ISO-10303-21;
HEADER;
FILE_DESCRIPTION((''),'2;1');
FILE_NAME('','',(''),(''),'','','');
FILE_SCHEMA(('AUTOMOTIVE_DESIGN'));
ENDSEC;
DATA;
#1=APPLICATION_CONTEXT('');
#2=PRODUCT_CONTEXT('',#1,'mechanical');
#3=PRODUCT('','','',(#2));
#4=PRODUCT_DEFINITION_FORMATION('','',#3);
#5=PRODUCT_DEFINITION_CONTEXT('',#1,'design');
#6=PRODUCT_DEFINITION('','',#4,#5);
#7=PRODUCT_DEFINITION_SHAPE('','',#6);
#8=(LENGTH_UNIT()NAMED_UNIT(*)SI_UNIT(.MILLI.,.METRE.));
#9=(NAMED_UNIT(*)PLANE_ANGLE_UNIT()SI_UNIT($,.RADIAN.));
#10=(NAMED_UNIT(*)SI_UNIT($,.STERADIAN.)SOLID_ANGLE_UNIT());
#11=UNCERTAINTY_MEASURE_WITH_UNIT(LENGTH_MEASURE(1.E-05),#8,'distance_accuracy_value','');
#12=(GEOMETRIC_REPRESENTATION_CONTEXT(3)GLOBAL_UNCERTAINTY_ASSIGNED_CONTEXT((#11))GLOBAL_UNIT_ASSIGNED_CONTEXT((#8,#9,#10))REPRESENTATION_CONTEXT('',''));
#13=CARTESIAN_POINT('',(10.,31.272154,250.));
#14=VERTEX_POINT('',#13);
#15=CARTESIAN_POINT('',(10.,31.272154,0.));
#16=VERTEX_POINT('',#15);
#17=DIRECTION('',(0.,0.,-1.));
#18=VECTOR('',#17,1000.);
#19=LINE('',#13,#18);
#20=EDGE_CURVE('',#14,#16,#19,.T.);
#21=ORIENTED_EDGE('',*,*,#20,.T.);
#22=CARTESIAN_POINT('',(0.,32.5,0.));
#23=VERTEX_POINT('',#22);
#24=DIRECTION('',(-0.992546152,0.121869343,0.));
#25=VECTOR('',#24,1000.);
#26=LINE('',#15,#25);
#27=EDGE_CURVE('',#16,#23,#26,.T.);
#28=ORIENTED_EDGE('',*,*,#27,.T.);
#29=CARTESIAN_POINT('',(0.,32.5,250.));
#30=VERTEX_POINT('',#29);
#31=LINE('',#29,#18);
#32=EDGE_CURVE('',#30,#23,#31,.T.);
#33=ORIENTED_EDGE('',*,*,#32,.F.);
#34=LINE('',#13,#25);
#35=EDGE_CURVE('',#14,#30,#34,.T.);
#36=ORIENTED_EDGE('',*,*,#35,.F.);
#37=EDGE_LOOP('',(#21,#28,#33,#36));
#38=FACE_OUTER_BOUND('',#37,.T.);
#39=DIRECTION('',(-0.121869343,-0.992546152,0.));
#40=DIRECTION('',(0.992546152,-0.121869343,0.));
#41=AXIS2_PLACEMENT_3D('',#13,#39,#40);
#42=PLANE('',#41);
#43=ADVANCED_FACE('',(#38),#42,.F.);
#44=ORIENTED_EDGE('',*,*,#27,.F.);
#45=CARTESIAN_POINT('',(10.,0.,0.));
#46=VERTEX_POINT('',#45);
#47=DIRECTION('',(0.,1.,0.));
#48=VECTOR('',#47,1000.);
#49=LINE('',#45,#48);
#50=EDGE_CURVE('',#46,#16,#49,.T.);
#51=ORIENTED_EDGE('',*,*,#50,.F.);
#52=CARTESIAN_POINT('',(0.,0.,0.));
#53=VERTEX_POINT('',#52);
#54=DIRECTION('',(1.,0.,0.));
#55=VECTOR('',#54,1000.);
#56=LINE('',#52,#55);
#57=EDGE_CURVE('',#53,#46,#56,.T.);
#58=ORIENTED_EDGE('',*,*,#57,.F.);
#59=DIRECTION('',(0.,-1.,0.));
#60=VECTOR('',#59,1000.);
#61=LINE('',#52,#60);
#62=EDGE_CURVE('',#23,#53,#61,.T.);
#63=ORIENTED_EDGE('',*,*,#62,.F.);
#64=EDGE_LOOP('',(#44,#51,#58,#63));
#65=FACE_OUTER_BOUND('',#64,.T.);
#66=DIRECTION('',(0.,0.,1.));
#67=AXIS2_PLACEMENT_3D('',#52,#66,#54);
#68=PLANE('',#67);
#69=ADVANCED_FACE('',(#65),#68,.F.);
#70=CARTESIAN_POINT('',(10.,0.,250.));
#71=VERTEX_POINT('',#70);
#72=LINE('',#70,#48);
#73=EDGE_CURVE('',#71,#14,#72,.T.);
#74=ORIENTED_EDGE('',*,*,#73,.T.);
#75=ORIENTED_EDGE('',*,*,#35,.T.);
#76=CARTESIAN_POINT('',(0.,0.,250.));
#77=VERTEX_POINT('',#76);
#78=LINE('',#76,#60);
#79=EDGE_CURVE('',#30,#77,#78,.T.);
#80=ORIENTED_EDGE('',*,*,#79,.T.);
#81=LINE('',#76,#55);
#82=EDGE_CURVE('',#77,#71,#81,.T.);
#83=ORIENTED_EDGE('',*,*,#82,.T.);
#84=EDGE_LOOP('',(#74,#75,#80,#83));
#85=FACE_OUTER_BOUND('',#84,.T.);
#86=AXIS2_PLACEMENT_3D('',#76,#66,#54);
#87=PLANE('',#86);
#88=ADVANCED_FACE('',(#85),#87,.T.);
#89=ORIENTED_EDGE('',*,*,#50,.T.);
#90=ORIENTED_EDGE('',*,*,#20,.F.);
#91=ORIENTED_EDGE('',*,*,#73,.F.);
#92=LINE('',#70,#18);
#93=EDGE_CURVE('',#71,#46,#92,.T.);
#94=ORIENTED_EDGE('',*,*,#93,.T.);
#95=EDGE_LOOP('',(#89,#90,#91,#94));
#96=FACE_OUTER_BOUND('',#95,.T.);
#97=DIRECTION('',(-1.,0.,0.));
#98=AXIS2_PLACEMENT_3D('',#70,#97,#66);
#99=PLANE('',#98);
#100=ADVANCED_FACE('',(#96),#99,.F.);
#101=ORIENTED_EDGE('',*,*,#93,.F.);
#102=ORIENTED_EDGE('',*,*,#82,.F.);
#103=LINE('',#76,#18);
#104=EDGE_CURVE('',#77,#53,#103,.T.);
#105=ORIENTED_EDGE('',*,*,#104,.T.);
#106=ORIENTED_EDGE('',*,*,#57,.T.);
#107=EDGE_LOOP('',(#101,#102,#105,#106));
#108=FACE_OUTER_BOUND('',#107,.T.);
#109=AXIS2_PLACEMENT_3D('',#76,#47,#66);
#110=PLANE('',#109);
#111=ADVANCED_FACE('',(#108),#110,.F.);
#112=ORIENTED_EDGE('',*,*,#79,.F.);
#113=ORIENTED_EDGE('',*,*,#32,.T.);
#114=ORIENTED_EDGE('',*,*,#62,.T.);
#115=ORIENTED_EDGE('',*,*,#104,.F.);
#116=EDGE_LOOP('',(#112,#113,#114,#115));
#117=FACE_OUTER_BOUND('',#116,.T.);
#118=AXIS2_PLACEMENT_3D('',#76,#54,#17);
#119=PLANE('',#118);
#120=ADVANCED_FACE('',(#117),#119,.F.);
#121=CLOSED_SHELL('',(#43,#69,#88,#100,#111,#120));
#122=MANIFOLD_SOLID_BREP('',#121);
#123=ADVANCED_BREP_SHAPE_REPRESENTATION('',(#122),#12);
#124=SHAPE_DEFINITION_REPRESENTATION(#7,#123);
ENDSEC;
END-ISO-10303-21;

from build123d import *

# Parameters (mm, degrees)
BOSS_EXTRUDE1_DEPTH = 250


with BuildPart() as part:
    # Sketch1 → Boss-Extrude1 (new body)
    with BuildSketch(Plane.XY):
        Polygon((0, 0), (0, 32.5), (10, 31.272154391), (10, 0), align=None)
    extrude(amount=BOSS_EXTRUDE1_DEPTH)


solid = part.part
